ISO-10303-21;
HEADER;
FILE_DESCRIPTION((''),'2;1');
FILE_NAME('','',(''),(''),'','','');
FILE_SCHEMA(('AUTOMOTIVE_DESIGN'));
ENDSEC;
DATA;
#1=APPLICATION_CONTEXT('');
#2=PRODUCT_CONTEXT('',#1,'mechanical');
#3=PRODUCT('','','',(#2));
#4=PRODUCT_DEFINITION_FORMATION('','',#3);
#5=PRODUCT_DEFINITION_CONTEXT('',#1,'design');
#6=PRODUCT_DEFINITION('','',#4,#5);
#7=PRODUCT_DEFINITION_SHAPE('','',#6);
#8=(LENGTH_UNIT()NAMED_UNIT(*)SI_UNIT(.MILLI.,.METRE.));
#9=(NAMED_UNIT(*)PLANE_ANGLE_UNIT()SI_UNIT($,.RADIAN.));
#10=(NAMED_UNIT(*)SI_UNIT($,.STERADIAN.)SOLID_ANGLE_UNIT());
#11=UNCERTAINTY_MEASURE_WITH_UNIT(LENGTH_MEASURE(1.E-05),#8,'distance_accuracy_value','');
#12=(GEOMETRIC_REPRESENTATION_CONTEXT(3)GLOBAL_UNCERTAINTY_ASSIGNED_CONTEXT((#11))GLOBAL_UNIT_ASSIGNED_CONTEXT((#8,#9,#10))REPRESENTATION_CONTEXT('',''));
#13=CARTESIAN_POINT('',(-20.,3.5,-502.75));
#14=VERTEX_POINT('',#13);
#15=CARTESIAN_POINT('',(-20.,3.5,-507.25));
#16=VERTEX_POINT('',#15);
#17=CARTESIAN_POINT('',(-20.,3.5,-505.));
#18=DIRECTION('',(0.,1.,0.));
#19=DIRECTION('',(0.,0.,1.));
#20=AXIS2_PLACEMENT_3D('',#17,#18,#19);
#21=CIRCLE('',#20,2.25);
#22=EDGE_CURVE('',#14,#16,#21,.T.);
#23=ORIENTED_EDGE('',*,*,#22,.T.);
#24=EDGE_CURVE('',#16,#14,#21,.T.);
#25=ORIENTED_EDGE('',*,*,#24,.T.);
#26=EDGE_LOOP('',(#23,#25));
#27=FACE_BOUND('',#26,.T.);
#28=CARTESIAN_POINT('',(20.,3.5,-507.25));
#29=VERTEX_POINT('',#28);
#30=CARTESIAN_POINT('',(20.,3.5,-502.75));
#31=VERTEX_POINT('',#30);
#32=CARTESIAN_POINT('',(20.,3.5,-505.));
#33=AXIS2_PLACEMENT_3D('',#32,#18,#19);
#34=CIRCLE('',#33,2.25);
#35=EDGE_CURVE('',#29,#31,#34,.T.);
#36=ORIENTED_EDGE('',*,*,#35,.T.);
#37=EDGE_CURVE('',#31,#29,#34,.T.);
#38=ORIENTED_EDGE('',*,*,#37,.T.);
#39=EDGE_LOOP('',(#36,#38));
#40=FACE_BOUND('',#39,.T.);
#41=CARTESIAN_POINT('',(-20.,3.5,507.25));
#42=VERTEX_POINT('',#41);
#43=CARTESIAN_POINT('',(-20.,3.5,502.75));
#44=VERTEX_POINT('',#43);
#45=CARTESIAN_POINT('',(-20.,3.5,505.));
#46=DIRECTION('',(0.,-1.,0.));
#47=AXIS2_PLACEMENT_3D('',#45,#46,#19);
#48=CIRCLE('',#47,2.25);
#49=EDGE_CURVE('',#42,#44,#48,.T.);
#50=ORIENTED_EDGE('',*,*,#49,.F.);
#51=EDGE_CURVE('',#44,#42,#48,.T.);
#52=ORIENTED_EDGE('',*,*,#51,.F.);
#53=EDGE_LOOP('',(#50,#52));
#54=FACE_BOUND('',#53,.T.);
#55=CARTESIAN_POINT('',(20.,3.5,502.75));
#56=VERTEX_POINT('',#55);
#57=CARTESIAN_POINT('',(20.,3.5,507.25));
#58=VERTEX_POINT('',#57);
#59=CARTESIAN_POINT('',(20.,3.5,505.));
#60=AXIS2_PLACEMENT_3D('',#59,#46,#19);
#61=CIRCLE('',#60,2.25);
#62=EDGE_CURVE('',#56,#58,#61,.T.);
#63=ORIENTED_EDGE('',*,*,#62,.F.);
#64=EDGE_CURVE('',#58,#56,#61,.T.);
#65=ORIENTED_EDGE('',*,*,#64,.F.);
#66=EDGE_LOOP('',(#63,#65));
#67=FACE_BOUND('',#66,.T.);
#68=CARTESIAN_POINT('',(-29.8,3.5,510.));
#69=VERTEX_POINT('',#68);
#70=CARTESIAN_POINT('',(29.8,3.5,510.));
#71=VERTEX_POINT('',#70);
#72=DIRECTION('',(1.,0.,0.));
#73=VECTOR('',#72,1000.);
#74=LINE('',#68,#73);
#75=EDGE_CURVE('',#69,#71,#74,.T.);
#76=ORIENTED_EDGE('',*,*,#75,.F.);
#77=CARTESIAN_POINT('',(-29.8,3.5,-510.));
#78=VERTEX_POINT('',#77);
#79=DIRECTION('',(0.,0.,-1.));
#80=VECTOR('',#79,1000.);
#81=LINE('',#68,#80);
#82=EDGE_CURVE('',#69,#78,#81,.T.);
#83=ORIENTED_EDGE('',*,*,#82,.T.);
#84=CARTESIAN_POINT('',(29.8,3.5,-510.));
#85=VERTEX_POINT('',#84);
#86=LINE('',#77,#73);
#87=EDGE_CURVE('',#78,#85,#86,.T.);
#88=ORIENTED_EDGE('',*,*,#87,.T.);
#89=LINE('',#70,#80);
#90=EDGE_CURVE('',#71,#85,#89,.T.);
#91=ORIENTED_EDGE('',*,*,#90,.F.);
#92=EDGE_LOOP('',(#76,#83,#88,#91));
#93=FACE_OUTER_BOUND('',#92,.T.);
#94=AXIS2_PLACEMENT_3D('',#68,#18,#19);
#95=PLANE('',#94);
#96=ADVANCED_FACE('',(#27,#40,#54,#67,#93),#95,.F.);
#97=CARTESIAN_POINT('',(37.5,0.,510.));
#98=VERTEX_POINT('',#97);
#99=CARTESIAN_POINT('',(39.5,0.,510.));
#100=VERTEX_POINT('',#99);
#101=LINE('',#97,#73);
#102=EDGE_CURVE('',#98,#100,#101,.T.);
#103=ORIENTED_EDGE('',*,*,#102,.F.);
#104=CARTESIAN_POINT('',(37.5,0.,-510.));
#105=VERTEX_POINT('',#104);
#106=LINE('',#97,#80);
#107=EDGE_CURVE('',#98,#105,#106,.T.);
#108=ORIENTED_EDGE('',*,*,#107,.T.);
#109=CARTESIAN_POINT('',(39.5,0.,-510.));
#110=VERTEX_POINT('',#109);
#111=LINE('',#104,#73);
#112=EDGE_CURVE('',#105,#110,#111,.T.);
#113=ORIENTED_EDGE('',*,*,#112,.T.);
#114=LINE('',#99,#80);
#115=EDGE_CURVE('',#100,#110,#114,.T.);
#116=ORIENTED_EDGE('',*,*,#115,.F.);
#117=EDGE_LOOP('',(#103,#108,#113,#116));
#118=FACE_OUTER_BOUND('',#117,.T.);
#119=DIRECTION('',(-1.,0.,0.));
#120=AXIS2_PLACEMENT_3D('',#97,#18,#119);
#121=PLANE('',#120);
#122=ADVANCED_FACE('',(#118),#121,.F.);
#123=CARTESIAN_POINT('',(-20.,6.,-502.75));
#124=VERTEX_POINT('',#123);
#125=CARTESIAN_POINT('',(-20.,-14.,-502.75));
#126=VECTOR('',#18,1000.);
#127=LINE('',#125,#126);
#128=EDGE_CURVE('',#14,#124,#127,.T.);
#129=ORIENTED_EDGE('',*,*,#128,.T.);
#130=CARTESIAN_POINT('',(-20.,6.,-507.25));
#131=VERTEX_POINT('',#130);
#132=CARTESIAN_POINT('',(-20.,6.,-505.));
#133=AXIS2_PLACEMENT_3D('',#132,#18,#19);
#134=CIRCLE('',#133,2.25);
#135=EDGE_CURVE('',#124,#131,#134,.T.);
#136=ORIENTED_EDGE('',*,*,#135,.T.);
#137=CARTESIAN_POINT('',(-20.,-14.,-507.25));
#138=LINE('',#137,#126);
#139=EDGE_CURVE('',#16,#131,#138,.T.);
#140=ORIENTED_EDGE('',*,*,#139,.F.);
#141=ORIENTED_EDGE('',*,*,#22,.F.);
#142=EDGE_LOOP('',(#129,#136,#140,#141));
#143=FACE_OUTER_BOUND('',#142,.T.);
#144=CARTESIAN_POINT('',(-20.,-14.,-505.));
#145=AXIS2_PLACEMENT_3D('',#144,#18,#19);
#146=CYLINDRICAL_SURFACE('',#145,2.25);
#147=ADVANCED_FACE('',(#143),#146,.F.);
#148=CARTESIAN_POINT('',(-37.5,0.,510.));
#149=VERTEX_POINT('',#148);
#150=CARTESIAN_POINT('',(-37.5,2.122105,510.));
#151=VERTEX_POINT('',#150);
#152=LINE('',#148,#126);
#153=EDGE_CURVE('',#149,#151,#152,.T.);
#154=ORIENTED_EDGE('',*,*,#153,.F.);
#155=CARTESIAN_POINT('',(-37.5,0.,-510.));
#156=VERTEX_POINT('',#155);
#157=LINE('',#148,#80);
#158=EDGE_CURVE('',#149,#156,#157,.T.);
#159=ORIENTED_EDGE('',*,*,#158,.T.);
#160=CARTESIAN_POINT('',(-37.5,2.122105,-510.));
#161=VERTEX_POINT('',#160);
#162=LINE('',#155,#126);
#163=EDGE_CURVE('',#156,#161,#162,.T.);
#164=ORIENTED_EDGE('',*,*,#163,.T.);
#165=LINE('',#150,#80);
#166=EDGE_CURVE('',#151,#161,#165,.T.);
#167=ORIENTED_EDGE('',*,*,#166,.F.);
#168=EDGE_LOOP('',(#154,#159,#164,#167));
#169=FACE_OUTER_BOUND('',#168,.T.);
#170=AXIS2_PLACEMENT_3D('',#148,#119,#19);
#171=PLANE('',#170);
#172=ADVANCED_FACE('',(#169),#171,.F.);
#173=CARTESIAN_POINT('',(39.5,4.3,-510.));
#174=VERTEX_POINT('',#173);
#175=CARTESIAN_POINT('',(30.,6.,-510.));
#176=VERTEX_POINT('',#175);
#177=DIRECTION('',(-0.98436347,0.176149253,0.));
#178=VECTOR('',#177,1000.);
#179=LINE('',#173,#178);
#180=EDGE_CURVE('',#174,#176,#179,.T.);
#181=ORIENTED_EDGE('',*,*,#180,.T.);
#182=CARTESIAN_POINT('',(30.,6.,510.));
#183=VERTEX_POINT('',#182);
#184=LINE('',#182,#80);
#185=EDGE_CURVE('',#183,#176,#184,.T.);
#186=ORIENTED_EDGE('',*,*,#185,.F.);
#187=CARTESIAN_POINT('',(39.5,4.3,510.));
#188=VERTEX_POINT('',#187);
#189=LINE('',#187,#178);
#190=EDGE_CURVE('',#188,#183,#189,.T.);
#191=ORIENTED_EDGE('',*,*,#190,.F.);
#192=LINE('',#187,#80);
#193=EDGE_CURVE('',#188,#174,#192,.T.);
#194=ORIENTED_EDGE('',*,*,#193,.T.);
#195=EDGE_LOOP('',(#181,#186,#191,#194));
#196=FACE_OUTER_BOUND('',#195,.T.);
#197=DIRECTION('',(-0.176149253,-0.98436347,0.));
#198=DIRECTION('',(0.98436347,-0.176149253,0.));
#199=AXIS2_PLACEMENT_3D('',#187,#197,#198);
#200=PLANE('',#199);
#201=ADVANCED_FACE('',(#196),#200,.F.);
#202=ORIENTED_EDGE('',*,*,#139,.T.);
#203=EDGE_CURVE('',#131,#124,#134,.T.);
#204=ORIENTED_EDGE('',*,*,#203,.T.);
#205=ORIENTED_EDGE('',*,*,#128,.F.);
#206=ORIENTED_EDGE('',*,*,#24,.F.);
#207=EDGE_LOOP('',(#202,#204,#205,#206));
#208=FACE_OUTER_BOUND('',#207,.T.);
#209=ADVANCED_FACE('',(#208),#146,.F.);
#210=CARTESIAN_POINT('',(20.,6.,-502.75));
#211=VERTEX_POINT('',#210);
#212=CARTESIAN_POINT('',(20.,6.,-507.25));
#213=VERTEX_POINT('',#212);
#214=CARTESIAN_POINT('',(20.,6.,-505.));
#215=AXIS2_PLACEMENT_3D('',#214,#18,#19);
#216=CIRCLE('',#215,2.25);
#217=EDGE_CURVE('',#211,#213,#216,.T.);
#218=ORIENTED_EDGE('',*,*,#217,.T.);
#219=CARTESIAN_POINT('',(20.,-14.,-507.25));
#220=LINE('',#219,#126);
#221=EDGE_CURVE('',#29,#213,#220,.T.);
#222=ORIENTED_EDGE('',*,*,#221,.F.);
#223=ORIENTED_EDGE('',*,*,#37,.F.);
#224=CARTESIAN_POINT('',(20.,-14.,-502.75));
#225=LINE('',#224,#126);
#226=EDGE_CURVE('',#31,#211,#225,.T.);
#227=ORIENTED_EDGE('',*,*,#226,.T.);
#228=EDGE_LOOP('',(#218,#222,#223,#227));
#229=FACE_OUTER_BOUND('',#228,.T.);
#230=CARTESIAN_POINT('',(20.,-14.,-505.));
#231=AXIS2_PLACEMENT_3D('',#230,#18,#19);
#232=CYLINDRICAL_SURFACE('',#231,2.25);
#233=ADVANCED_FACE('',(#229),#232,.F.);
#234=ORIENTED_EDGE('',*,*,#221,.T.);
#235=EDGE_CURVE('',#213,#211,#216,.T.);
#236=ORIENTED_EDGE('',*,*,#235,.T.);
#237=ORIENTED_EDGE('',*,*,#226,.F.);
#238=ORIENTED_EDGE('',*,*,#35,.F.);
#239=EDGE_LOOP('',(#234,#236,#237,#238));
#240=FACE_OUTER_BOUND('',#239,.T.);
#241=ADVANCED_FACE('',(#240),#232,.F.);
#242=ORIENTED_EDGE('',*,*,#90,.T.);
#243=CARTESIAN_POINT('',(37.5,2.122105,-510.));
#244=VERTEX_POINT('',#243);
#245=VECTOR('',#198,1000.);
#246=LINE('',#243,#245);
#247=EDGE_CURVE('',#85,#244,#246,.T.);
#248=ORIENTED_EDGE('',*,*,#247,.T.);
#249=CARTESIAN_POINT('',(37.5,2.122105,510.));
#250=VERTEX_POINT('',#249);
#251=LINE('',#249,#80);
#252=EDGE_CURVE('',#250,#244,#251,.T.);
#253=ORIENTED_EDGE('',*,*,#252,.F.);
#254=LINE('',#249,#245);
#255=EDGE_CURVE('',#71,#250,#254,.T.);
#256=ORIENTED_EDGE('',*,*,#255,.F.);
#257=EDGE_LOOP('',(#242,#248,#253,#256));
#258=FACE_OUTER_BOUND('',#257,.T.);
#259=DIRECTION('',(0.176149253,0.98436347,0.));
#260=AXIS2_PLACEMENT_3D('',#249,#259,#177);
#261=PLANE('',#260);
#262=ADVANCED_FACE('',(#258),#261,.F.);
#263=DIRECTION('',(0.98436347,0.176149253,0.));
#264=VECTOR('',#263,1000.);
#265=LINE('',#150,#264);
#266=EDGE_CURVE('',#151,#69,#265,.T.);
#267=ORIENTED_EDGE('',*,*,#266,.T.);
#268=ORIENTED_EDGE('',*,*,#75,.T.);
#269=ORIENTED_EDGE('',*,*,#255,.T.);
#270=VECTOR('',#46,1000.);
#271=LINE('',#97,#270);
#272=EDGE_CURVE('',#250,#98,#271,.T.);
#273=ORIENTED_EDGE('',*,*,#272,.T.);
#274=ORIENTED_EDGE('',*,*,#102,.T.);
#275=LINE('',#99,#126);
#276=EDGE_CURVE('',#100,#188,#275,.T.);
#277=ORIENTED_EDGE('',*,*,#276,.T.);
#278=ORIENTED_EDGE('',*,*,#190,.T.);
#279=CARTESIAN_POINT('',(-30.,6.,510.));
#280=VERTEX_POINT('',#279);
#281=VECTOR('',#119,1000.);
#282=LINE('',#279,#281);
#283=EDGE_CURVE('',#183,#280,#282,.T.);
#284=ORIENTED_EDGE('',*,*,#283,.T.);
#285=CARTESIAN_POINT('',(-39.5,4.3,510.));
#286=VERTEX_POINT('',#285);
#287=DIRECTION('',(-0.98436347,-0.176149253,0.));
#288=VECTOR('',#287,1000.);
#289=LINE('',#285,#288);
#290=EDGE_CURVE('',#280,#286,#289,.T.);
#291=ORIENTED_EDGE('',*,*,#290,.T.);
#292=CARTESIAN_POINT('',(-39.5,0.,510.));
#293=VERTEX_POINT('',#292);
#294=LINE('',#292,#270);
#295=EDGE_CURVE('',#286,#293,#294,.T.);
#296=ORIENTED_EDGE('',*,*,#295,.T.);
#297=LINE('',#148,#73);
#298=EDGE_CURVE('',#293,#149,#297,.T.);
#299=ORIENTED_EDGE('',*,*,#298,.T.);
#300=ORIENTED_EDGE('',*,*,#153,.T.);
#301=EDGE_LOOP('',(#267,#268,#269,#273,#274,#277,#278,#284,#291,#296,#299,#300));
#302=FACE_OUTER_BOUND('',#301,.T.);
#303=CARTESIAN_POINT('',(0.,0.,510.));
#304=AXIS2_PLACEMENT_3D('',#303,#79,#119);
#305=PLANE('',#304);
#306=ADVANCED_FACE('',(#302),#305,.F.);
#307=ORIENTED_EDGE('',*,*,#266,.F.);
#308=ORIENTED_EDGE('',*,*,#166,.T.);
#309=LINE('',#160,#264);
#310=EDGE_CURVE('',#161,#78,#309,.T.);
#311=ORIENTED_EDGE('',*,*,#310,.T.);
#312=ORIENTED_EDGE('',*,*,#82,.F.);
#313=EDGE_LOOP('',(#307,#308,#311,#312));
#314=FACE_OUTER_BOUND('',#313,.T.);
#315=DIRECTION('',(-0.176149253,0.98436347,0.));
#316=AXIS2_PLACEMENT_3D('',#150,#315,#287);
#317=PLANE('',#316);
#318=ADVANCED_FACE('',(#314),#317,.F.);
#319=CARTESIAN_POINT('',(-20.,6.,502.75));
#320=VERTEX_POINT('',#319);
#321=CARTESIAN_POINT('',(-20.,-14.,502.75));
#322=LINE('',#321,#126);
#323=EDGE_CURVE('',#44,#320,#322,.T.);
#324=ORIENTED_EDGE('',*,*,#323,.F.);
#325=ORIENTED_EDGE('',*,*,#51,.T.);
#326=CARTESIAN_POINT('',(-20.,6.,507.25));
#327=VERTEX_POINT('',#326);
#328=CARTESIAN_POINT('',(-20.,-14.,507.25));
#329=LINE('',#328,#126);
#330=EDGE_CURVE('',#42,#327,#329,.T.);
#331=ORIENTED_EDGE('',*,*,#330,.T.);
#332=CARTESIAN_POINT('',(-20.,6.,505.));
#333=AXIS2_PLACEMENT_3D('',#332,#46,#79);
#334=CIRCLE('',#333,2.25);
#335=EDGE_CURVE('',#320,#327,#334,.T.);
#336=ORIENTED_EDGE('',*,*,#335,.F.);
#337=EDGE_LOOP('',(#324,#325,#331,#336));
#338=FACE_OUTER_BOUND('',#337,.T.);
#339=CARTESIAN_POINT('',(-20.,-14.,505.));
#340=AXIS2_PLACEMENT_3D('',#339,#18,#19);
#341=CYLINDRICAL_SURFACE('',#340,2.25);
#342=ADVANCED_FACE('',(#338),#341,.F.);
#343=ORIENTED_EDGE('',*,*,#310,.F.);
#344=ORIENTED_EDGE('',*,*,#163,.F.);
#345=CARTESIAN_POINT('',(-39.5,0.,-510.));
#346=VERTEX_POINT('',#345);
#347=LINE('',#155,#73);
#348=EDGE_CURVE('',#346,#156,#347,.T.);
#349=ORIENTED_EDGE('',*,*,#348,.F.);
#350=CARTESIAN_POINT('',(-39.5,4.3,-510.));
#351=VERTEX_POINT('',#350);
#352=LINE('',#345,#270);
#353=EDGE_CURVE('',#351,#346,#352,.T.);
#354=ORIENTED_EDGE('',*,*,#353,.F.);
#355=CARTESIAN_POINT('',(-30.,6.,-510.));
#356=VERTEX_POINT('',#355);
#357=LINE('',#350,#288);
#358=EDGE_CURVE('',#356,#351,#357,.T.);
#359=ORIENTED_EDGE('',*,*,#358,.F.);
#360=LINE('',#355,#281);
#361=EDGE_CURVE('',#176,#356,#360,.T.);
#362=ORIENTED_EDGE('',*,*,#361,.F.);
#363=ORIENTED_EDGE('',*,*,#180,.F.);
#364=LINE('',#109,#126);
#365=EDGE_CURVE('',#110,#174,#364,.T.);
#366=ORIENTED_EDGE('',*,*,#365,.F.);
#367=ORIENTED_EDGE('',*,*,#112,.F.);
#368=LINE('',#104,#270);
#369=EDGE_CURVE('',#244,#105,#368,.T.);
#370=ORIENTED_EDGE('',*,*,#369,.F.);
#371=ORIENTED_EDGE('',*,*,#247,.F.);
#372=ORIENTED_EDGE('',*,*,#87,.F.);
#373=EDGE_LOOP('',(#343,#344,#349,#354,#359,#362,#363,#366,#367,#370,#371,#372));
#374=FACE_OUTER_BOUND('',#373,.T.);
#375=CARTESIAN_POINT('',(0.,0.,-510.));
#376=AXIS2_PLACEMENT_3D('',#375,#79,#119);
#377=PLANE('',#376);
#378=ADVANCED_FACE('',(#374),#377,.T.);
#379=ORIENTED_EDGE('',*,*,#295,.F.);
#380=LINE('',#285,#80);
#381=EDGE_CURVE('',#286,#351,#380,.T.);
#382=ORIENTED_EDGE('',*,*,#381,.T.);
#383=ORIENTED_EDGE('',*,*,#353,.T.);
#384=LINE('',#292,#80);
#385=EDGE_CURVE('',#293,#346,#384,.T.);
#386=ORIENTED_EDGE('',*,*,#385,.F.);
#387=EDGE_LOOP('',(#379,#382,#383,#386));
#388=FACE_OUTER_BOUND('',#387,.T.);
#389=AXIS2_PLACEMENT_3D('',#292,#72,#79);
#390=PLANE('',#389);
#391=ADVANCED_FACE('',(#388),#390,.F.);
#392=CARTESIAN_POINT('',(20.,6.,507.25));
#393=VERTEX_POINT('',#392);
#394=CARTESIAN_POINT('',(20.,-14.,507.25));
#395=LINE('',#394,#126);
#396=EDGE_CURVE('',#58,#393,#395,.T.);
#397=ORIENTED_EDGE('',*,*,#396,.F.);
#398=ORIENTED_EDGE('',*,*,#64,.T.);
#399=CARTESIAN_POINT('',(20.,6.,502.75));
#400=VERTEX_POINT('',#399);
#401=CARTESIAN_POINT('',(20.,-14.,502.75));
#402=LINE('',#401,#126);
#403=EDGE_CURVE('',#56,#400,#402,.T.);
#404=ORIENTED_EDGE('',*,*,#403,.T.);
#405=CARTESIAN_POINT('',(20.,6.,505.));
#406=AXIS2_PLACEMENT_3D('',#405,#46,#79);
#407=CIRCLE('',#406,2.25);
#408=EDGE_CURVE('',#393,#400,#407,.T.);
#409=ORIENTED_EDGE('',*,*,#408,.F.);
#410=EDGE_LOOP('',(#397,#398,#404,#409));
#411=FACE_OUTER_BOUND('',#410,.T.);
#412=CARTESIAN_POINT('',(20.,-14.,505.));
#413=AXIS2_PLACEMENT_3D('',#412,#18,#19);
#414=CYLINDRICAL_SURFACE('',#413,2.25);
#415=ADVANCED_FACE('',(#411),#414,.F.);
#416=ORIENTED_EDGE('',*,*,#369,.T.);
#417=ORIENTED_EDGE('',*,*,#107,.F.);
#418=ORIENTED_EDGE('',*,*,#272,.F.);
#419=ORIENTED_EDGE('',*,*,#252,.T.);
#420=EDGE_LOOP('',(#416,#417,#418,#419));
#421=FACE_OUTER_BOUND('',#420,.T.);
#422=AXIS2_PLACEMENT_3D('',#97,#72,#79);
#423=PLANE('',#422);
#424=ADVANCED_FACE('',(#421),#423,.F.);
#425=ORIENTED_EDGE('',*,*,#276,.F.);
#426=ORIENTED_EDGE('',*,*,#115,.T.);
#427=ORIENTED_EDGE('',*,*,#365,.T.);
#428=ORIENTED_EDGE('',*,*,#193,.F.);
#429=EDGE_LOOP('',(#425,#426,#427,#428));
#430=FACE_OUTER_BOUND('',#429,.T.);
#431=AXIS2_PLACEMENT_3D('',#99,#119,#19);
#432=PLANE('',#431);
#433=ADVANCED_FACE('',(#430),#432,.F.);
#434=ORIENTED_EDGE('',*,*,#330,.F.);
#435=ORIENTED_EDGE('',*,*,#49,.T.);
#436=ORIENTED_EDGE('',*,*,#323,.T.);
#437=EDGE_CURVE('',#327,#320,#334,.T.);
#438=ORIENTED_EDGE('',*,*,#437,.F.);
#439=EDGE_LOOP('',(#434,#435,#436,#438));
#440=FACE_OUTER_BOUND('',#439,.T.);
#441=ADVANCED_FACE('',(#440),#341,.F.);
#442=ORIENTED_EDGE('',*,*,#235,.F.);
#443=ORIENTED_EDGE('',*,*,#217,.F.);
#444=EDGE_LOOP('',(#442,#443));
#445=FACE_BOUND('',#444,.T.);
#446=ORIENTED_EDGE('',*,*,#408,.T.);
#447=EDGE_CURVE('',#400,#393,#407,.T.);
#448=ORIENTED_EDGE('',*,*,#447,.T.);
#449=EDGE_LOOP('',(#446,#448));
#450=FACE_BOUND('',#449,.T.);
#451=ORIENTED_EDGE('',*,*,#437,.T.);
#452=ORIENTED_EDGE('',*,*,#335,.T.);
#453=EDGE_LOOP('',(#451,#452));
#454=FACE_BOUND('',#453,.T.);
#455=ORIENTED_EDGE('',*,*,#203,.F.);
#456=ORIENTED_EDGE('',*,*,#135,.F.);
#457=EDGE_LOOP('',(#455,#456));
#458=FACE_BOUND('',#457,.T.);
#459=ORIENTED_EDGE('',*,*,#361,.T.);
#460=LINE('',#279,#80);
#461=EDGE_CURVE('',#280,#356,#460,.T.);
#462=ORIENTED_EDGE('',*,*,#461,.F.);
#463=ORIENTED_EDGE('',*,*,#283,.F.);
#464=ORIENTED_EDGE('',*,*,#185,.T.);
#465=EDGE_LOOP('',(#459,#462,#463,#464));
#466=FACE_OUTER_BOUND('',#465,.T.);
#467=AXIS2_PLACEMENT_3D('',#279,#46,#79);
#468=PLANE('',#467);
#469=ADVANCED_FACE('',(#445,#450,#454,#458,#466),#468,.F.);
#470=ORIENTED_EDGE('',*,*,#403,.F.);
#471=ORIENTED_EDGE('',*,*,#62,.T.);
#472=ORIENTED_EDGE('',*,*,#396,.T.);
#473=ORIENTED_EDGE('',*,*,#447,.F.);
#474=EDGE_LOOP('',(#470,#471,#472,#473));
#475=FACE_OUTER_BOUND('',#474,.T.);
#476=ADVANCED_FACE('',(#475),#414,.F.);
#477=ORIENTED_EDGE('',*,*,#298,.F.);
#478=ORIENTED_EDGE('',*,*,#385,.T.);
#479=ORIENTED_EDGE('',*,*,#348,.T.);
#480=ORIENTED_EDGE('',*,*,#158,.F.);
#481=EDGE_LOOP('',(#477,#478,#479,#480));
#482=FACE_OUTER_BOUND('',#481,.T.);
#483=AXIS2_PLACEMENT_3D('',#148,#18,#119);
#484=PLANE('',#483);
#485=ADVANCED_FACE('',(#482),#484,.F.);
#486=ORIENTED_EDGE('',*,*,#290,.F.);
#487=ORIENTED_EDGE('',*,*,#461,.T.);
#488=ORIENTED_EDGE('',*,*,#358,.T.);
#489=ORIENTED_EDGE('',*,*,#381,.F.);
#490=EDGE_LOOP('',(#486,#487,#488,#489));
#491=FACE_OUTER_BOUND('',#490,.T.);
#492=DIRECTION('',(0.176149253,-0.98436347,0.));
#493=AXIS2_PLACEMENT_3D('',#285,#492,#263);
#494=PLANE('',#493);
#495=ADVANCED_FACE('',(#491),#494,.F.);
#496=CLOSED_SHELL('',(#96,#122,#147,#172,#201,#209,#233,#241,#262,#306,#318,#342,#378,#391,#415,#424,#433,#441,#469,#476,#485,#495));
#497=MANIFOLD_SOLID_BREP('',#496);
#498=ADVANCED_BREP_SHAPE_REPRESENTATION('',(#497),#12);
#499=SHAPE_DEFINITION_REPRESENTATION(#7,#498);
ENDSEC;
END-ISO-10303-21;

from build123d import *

# Parameters (mm, degrees)
EXTRUDE_1_DEPTH     = 510
SKETCH_2_R          = 2.25
CUT_EXTRUDE_1_DEPTH = 20


with BuildPart() as part:
    # 草图1 → 凸台-拉伸1 (new, symmetric)
    with BuildSketch(Plane.XY):
        Polygon((-37.5, 0), (-39.5, 0), (-39.5, 4.3), (-30, 6), (30, 6), (39.5, 4.3), (39.5, 0), (37.5, 0), (37.5, 2.122105263), (29.8, 3.5), (-29.8, 3.5), (-37.5, 2.122105263), align=None)
    extrude(amount=EXTRUDE_1_DEPTH, both=True)

    # 草图2 → 切除-拉伸1 (cut)
    with BuildSketch(Plane(origin=(0, 6, 0), x_dir=(1, 0, 0), z_dir=(0, 1, 0))):
        with Locations(Location((-20, 505, 0), (0, 0, 270))):
            Circle(SKETCH_2_R)
        with Locations(Location((20, 505, 0), (0, 0, 270))):
            Circle(SKETCH_2_R)
    cut_extrude_1 = extrude(amount=-CUT_EXTRUDE_1_DEPTH, mode=Mode.SUBTRACT)

    # 镜向1: 切除-拉伸1 across plane
    add(cut_extrude_1.mirror(Plane.XY), mode=Mode.SUBTRACT)


solid = part.part
